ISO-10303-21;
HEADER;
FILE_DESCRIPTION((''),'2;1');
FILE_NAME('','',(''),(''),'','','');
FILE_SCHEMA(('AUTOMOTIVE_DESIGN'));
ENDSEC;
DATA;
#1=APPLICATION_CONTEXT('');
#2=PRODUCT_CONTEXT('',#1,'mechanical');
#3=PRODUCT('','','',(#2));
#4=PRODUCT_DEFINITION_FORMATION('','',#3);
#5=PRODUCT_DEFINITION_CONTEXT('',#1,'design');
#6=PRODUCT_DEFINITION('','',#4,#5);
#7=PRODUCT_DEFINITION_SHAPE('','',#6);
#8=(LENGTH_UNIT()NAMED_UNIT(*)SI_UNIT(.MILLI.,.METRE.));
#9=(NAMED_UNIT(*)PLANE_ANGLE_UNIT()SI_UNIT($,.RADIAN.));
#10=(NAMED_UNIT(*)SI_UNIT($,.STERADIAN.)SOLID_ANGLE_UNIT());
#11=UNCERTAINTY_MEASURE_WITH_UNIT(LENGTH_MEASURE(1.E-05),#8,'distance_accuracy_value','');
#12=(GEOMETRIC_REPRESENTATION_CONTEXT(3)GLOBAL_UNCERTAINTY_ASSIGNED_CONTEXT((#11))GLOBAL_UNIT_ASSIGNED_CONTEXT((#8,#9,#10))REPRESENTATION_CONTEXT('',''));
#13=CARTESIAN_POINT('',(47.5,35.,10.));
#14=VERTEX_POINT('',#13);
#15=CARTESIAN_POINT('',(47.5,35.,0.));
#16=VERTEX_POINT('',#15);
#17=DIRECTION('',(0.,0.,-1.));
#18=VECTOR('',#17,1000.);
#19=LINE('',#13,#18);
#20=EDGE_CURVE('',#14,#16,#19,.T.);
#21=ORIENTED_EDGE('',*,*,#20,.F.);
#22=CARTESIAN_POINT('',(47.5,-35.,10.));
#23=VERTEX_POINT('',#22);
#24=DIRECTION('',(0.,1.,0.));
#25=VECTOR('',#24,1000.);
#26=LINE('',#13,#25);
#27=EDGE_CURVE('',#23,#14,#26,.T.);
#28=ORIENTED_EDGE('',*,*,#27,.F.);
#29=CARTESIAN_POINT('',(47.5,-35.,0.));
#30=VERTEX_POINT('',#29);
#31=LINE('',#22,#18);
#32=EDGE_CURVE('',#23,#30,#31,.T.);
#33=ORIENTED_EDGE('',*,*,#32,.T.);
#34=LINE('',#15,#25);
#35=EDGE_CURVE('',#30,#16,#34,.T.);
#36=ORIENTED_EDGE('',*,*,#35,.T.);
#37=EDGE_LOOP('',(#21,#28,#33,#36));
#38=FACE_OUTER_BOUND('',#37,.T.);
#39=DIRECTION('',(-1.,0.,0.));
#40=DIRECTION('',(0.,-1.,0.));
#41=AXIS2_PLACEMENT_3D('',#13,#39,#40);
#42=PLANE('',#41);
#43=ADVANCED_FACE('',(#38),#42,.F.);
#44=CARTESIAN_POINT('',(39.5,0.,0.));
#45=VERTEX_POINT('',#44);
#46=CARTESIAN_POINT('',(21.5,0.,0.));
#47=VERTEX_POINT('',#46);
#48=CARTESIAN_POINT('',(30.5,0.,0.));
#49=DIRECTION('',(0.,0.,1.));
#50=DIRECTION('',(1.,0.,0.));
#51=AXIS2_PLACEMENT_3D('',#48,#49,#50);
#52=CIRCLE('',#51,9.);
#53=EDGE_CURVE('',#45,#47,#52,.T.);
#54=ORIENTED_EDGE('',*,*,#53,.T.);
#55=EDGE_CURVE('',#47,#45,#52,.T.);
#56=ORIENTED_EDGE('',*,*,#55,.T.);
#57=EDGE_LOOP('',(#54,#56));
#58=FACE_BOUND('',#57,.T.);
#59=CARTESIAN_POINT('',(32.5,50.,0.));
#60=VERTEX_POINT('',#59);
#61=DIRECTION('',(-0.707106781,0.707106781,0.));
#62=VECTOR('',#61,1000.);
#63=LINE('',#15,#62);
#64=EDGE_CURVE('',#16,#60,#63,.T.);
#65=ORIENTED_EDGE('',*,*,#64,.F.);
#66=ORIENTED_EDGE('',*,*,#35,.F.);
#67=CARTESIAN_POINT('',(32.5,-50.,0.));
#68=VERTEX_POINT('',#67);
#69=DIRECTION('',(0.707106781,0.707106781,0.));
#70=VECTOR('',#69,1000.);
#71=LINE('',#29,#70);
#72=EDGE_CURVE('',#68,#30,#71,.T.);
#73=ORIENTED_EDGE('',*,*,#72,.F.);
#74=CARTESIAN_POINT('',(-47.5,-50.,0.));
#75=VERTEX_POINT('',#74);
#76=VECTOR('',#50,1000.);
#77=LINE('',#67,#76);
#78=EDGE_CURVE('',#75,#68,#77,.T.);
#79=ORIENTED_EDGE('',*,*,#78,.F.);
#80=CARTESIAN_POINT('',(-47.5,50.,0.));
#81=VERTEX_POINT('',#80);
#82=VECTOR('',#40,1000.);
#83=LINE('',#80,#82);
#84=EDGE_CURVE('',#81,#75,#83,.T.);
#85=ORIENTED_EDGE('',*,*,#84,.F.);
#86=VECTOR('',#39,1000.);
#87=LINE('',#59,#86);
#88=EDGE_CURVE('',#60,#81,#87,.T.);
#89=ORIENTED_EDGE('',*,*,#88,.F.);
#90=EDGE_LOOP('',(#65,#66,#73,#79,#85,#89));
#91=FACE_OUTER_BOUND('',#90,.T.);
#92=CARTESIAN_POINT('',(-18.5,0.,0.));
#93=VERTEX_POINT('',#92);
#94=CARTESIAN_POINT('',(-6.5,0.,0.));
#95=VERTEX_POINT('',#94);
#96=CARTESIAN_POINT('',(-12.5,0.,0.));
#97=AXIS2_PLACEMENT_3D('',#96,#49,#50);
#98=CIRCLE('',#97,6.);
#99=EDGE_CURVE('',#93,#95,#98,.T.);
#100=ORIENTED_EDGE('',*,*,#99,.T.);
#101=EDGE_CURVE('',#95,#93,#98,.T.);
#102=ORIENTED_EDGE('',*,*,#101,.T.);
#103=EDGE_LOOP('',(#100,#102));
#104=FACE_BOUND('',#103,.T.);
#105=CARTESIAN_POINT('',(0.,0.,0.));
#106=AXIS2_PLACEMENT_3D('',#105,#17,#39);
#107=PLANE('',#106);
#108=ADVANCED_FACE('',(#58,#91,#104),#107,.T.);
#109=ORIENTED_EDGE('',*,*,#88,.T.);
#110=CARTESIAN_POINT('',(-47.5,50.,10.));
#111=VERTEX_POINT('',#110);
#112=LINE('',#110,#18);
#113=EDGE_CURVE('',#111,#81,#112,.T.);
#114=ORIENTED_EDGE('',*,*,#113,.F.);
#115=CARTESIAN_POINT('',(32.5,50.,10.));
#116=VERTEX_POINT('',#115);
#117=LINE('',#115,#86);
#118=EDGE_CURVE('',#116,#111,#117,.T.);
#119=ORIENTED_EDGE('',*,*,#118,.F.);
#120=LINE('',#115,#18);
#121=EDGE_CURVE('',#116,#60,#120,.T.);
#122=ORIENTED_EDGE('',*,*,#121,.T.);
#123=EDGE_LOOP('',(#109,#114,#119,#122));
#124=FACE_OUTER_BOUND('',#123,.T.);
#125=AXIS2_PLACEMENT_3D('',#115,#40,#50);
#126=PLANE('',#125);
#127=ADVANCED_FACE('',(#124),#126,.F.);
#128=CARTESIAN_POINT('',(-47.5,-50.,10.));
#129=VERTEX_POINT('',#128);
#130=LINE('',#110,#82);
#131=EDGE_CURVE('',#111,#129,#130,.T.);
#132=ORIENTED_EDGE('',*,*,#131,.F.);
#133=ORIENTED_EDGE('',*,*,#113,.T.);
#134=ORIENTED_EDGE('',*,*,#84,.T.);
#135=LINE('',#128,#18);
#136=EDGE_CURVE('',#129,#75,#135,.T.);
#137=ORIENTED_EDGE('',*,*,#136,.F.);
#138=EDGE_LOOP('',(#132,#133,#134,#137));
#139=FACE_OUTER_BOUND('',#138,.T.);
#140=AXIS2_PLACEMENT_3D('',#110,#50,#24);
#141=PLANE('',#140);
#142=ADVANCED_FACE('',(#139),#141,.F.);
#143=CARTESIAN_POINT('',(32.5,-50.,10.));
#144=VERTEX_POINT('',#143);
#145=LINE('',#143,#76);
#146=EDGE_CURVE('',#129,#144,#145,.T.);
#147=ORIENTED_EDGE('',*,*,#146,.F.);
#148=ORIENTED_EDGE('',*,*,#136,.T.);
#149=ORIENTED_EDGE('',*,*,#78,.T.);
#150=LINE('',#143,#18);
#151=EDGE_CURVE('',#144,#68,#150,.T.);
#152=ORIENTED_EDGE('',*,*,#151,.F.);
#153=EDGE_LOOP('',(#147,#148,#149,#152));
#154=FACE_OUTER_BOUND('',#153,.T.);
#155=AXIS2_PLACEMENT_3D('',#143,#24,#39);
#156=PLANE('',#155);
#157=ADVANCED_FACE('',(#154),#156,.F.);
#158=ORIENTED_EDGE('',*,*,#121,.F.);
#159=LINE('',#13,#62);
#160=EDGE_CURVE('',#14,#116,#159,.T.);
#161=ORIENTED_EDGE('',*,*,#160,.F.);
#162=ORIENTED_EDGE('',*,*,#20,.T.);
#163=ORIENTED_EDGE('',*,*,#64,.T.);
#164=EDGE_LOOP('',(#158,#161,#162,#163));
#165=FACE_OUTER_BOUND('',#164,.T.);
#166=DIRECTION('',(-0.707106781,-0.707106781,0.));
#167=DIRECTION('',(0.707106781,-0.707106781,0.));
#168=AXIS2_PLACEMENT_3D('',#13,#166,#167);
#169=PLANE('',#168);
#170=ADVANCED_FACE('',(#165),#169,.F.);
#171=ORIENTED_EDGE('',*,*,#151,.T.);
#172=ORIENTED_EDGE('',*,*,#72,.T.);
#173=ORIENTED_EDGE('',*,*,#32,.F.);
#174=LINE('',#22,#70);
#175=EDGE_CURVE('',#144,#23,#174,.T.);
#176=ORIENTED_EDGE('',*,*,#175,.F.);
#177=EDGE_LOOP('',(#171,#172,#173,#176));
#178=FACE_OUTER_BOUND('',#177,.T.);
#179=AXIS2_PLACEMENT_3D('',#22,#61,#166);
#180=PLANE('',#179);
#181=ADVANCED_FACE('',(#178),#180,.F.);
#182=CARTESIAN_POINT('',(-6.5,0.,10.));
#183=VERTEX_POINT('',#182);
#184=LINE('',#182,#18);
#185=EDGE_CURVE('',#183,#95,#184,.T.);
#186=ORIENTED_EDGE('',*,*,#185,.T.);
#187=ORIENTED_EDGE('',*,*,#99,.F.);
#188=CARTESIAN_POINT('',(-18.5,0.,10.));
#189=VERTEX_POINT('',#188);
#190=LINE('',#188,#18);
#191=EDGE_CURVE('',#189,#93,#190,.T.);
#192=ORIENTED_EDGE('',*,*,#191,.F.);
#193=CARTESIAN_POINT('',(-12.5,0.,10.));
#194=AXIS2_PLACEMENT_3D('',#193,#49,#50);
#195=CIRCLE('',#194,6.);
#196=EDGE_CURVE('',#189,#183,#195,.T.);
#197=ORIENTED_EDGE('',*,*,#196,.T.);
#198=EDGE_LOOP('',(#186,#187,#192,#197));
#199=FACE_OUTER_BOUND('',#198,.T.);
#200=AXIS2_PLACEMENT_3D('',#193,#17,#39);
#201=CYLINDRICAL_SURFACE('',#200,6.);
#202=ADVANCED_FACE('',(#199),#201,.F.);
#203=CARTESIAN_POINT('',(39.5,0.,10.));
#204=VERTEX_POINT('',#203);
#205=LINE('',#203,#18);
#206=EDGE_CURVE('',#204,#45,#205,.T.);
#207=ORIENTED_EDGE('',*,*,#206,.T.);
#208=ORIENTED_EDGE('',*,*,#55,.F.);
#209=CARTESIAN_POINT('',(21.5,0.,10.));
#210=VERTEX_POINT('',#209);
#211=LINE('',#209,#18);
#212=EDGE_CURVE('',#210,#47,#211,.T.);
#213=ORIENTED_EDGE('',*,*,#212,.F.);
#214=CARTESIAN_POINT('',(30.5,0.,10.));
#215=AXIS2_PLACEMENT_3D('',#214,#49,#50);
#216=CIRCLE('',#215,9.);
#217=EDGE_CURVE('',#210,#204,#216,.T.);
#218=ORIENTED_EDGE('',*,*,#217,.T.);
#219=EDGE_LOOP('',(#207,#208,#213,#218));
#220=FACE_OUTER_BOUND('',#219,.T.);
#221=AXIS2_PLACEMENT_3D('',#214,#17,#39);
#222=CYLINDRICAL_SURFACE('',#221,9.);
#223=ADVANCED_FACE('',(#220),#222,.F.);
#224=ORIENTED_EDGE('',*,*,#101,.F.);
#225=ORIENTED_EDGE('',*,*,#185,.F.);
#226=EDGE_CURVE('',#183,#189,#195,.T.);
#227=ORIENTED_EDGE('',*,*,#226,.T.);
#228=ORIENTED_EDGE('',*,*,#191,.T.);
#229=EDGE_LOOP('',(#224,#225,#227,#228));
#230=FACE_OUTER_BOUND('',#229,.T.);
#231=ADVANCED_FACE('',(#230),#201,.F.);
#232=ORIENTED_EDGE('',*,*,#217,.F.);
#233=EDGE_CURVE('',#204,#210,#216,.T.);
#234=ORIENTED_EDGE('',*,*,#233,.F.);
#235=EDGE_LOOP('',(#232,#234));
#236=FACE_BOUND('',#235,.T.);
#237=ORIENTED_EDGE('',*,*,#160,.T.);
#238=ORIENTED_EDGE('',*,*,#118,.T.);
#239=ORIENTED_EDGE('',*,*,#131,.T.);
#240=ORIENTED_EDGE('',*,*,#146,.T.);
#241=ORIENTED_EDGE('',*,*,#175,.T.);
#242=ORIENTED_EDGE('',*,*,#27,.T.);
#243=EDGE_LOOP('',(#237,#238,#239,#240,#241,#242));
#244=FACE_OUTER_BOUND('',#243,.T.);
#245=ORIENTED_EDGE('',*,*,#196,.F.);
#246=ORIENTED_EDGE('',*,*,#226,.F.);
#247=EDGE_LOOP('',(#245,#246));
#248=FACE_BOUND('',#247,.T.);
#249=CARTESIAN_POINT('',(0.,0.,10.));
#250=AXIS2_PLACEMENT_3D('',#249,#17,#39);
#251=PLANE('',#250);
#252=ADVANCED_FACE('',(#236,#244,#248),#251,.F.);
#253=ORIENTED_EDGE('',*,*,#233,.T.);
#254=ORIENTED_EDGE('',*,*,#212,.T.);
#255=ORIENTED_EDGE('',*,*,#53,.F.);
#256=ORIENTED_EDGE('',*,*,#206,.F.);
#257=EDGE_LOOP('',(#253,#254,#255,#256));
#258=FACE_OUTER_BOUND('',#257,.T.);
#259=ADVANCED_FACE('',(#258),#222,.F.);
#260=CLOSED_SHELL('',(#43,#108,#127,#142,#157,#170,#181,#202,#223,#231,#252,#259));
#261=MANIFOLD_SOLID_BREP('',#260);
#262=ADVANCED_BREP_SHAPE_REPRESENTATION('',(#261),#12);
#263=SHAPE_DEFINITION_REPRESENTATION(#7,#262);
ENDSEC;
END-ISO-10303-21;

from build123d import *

# Parameters (mm, degrees)
SKETCH_1_R      = 6
SKETCH_1_R_2    = 9
EXTRUDE_1_DEPTH = 10


with BuildPart() as part:
    # 草图1 → 凸台-拉伸1 (new body)
    with BuildSketch(Plane.XY):
        Polygon((47.5, 35), (32.5, 50), (-47.5, 50), (-47.5, -50), (32.5, -50), (47.5, -35), align=None)
        with Locations((-12.5, 0)):
            Circle(SKETCH_1_R, mode=Mode.SUBTRACT)
        with Locations((30.5, 0)):
            Circle(SKETCH_1_R_2, mode=Mode.SUBTRACT)
    extrude(amount=EXTRUDE_1_DEPTH)


solid = part.part
